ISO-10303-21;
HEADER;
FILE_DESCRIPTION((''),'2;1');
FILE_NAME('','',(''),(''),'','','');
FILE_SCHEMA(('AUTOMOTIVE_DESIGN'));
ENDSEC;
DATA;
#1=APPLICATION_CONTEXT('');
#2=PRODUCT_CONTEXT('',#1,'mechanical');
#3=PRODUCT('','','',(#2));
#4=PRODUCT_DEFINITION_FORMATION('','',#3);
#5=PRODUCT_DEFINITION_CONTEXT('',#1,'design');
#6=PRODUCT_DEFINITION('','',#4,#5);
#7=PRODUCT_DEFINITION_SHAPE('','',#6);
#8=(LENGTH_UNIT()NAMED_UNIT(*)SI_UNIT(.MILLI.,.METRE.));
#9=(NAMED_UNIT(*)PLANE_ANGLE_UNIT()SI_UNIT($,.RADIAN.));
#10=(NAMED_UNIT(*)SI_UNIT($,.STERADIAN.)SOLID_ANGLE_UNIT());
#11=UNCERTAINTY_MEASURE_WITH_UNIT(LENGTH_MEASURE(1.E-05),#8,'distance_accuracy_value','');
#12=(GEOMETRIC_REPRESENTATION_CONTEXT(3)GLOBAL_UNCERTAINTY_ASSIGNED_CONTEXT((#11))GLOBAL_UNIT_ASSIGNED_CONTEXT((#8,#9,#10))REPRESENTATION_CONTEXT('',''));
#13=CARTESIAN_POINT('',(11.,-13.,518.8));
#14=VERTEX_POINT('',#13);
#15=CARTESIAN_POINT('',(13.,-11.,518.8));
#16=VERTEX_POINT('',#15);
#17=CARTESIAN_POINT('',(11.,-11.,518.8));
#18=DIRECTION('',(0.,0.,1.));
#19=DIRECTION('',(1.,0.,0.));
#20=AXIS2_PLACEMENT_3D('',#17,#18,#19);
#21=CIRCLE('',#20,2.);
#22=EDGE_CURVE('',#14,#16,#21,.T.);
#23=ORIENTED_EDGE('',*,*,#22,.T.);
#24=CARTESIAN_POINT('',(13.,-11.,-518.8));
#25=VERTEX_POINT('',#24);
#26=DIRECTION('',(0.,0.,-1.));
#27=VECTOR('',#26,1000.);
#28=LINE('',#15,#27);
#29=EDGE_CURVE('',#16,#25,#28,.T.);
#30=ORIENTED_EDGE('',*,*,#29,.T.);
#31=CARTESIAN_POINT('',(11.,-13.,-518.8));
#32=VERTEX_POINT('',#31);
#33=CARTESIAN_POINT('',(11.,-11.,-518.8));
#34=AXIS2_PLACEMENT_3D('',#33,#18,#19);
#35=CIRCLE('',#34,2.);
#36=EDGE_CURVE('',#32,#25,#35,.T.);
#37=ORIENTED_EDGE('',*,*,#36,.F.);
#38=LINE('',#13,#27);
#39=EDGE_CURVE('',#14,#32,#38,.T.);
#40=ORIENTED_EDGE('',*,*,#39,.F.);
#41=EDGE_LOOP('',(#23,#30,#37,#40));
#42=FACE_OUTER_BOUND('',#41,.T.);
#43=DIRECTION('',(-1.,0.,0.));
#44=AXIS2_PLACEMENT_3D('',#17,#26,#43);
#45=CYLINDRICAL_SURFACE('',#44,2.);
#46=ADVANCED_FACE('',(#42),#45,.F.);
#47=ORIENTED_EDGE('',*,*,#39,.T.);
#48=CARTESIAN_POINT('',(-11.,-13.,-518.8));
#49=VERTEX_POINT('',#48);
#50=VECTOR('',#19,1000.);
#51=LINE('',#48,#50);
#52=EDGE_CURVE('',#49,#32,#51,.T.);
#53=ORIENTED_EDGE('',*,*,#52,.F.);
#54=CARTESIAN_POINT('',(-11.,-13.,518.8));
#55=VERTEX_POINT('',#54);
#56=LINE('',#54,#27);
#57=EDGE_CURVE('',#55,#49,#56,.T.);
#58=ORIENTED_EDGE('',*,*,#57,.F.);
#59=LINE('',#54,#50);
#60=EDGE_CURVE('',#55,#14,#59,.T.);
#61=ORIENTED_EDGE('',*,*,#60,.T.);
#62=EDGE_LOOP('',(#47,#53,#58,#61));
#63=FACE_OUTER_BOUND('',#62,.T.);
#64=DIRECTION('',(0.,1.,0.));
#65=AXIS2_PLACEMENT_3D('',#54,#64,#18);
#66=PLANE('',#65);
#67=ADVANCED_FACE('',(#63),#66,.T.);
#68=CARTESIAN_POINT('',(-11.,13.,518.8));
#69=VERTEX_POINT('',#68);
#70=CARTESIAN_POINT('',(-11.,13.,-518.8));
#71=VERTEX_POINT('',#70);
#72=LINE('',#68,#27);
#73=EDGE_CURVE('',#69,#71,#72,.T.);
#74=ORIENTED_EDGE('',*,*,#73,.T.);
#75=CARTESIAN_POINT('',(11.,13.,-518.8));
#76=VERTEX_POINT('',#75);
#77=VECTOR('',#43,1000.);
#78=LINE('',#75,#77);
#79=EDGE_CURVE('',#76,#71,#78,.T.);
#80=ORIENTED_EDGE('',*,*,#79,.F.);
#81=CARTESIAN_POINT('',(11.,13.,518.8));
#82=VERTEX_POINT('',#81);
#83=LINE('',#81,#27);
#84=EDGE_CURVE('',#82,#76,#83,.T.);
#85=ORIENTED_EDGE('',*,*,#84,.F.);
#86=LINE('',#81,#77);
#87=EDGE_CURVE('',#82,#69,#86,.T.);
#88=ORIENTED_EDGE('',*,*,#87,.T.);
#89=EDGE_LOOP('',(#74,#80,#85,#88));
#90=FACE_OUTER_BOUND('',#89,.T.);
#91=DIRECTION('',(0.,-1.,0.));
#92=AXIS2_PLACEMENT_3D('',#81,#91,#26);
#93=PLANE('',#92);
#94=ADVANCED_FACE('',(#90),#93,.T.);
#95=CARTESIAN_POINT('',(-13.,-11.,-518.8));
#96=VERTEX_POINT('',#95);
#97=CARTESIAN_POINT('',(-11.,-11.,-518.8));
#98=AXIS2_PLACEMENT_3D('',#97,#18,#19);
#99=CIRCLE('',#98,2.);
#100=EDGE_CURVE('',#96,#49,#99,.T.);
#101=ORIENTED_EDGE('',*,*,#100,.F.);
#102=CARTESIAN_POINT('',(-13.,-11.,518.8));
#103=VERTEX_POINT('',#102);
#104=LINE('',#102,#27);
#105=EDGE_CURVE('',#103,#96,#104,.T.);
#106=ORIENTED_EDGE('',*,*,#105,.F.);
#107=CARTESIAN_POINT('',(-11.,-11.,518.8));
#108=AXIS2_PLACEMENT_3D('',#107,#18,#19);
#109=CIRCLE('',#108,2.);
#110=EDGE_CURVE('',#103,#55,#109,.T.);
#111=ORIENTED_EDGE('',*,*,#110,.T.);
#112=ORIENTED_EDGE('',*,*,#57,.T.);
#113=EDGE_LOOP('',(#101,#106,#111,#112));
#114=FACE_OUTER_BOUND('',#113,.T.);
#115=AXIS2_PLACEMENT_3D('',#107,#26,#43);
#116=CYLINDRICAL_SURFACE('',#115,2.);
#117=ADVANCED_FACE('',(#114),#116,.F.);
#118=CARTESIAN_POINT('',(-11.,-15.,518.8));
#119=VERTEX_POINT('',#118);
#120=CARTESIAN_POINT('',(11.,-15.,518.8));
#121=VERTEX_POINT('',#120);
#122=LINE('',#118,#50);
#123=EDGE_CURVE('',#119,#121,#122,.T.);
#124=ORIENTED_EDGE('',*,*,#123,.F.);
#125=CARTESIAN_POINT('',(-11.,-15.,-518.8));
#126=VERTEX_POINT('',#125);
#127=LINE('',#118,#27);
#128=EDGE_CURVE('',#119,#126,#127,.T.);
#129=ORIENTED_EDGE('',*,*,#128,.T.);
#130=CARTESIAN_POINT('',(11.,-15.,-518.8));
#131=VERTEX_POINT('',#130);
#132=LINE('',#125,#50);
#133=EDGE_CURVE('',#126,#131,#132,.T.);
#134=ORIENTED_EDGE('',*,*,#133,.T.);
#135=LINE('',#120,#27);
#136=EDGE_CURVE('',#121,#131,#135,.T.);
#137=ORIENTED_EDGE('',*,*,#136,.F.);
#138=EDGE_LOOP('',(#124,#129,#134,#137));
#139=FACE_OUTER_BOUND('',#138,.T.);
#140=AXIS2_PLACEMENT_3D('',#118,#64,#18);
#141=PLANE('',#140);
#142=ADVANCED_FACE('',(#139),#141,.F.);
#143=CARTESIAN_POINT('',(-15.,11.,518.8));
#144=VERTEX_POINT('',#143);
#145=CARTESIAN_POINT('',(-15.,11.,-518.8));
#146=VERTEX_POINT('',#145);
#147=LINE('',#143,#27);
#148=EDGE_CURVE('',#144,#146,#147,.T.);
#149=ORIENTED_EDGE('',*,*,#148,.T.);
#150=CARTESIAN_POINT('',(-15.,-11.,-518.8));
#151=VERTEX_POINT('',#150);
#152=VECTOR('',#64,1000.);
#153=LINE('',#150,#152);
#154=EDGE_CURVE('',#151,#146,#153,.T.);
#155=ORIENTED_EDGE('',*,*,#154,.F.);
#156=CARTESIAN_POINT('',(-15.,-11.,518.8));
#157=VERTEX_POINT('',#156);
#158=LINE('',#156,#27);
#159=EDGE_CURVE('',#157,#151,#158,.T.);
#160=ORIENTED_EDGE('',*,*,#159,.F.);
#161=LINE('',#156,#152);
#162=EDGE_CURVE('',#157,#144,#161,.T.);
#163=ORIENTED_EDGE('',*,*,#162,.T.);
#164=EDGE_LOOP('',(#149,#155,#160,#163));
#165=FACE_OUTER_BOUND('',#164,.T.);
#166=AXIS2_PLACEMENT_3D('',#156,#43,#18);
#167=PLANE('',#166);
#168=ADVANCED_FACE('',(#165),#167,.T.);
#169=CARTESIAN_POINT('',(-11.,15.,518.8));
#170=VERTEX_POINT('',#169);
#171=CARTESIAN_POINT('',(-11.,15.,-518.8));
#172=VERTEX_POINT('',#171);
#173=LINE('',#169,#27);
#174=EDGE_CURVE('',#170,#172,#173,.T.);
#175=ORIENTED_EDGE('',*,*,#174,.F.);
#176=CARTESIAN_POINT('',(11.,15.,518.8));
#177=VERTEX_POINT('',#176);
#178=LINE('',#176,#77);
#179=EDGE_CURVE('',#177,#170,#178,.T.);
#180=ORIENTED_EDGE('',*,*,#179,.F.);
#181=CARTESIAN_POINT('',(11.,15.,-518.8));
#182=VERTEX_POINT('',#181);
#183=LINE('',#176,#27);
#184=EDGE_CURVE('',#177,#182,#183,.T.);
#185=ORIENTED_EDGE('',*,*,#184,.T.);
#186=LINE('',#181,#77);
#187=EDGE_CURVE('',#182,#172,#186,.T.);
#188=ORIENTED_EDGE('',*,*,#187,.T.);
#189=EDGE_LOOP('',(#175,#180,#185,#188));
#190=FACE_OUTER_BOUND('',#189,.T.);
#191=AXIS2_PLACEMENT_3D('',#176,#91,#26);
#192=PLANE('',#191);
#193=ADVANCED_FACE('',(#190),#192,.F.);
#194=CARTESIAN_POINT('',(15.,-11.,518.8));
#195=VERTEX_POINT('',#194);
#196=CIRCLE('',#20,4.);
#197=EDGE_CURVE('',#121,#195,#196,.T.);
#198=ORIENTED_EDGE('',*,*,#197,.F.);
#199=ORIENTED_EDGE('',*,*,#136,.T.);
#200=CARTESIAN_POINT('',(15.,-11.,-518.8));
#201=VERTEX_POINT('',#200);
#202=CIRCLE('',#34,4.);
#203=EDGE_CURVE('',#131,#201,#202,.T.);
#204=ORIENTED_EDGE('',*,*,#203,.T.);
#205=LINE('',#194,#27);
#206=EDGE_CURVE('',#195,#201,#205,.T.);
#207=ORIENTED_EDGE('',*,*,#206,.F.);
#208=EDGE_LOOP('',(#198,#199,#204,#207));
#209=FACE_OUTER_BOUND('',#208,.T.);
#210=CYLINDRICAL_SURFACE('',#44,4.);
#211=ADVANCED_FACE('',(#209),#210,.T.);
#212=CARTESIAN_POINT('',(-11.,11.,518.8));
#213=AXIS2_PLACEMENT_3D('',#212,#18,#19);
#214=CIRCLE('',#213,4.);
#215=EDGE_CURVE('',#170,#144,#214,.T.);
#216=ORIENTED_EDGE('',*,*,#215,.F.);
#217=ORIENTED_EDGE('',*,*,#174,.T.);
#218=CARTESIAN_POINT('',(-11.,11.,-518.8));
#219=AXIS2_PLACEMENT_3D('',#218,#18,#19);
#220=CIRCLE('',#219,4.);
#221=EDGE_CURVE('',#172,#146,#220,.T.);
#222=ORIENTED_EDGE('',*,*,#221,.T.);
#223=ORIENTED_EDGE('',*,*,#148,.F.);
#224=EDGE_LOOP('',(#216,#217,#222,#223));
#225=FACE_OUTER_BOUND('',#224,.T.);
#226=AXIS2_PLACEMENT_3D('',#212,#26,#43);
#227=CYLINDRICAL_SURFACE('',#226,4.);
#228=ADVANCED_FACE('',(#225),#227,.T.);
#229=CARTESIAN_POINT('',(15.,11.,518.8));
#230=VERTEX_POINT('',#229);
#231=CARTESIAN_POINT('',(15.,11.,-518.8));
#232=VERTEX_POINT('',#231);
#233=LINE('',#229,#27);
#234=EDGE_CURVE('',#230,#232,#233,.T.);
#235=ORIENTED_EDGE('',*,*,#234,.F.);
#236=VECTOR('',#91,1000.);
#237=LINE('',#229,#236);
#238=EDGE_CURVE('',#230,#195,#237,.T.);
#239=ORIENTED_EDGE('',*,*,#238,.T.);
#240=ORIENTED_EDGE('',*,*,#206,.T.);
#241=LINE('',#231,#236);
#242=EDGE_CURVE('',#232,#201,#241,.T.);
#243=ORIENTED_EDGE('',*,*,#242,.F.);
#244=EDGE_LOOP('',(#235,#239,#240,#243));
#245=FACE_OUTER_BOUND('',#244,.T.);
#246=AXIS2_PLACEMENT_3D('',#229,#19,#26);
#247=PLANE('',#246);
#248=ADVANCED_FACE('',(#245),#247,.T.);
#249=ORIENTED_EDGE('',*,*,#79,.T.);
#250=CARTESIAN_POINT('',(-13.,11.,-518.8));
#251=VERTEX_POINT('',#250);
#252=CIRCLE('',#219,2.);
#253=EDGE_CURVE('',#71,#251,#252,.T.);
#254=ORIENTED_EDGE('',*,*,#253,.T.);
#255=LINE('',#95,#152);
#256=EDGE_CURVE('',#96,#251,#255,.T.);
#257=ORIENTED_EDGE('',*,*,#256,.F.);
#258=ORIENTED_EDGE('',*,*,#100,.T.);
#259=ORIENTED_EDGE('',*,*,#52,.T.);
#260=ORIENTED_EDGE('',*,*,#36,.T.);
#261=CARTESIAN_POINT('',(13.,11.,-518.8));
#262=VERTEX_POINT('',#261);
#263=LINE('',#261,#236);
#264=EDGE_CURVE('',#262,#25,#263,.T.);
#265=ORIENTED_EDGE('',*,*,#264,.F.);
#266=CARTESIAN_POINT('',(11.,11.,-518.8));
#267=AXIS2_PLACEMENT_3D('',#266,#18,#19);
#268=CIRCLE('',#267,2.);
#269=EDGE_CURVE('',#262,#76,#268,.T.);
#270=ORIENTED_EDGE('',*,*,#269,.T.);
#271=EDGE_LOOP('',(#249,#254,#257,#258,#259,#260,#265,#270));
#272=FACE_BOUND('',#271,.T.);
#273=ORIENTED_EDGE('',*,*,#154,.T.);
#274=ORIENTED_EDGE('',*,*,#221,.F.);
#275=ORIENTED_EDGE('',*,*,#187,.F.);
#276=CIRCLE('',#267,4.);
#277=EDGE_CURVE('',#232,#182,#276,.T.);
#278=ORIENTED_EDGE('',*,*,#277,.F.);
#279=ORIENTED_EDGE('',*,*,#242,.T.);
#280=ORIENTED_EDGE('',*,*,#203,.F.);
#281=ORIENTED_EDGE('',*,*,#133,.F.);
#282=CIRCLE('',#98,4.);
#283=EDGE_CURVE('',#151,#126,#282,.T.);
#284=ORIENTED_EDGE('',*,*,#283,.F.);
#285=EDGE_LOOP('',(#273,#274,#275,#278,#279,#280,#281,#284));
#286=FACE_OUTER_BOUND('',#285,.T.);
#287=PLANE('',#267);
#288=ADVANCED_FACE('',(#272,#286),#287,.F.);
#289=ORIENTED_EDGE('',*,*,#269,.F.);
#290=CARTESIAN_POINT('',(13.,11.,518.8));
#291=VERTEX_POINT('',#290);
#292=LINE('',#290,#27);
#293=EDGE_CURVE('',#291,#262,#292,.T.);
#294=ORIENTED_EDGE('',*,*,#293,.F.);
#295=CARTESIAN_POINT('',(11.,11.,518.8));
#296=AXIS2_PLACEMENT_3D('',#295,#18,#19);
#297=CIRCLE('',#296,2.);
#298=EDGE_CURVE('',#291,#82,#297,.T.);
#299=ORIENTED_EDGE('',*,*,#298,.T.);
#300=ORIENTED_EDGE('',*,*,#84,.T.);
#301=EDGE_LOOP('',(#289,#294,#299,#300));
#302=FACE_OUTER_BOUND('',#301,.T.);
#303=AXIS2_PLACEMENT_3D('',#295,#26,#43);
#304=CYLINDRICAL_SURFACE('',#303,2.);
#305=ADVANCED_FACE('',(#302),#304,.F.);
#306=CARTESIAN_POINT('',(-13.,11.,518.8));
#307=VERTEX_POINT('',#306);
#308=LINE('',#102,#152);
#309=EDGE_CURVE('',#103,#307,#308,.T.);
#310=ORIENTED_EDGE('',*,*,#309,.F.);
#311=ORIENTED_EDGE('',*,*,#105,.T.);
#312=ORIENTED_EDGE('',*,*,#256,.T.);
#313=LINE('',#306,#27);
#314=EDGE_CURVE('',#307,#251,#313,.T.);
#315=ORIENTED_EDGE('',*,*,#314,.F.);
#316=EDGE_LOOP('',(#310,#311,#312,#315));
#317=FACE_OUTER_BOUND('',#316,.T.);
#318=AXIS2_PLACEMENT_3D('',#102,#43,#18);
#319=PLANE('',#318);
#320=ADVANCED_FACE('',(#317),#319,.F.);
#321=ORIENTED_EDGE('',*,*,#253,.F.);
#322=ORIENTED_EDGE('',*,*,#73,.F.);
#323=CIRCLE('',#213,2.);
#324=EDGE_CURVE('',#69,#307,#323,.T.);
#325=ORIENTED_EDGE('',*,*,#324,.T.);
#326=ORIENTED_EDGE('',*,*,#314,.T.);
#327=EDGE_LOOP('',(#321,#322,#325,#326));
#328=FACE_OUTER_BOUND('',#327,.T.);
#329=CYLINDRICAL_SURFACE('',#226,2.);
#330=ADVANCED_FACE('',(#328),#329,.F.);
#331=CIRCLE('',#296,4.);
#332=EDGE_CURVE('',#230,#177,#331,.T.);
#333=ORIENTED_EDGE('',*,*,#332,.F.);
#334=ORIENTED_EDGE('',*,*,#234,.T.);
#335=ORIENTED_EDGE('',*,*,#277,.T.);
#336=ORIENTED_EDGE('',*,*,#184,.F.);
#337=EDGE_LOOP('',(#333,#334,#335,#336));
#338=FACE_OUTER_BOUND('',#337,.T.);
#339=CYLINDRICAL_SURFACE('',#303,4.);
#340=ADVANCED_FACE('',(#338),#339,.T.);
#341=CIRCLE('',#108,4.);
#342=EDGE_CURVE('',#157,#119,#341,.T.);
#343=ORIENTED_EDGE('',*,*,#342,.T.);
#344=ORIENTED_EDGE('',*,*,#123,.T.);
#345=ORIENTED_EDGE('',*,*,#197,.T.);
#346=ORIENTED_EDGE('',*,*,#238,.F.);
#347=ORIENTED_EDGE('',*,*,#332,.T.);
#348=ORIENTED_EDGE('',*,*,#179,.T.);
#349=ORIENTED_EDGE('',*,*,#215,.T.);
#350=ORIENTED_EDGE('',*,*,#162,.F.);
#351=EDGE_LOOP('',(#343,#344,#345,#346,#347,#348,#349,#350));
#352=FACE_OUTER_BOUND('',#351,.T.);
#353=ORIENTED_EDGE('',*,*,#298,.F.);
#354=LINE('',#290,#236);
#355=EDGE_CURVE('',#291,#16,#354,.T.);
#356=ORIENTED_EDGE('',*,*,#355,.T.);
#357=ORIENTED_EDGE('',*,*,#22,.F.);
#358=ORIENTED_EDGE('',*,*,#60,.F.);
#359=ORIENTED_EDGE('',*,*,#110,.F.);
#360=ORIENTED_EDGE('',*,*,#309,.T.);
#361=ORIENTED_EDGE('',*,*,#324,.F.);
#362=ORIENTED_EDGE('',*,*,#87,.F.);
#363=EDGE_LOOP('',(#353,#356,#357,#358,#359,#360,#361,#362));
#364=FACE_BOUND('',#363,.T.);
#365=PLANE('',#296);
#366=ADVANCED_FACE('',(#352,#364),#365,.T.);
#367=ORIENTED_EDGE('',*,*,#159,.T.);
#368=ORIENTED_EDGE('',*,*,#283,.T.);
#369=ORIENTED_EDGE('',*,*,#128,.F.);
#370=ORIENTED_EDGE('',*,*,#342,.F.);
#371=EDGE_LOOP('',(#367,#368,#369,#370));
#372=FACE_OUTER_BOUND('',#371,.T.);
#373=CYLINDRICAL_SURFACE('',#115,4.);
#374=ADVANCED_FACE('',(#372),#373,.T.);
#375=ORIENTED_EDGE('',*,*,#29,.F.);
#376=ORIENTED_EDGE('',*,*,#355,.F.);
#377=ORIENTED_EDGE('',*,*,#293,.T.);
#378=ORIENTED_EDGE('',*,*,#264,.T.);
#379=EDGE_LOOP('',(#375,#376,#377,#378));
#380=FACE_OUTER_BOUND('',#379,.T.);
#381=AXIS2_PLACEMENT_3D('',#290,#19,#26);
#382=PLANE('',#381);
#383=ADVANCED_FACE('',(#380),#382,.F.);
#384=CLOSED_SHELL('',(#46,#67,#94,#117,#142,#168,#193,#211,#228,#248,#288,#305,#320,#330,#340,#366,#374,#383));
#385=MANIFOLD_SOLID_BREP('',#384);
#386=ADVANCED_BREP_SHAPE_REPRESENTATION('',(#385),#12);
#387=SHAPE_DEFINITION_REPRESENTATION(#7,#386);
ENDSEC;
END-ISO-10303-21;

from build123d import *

# Parameters (mm, degrees)
EXTRUDE_THIN1_DEPTH = 518.8


with BuildPart() as part:
    # Sketch1 → Extrude-Thin1 (new, symmetric)
    with BuildSketch(Plane.XY):
        with BuildLine():
            Line((-15, 11), (-15, -11))
            ThreePointArc((-15, -11), (-13.828427125, -13.828427125), (-11, -15))
            Line((-11, -15), (11, -15))
            ThreePointArc((11, -15), (13.828427125, -13.828427125), (15, -11))
            Line((15, -11), (15, 11))
            ThreePointArc((15, 11), (13.828427125, 13.828427125), (11, 15))
            Line((11, 15), (-11, 15))
            ThreePointArc((-11, 15), (-13.828427125, 13.828427125), (-15, 11))
        make_face()
        with BuildLine():
            Line((-13, 11), (-13, -11))
            ThreePointArc((-13, -11), (-12.414213562, -12.414213562), (-11, -13))
            Line((-11, -13), (11, -13))
            ThreePointArc((11, -13), (12.414213562, -12.414213562), (13, -11))
            Line((13, -11), (13, 11))
            ThreePointArc((13, 11), (12.414213562, 12.414213562), (11, 13))
            Line((11, 13), (-11, 13))
            ThreePointArc((-11, 13), (-12.414213562, 12.414213562), (-13, 11))
        make_face(mode=Mode.SUBTRACT)
    extrude(amount=EXTRUDE_THIN1_DEPTH, both=True)


solid = part.part
